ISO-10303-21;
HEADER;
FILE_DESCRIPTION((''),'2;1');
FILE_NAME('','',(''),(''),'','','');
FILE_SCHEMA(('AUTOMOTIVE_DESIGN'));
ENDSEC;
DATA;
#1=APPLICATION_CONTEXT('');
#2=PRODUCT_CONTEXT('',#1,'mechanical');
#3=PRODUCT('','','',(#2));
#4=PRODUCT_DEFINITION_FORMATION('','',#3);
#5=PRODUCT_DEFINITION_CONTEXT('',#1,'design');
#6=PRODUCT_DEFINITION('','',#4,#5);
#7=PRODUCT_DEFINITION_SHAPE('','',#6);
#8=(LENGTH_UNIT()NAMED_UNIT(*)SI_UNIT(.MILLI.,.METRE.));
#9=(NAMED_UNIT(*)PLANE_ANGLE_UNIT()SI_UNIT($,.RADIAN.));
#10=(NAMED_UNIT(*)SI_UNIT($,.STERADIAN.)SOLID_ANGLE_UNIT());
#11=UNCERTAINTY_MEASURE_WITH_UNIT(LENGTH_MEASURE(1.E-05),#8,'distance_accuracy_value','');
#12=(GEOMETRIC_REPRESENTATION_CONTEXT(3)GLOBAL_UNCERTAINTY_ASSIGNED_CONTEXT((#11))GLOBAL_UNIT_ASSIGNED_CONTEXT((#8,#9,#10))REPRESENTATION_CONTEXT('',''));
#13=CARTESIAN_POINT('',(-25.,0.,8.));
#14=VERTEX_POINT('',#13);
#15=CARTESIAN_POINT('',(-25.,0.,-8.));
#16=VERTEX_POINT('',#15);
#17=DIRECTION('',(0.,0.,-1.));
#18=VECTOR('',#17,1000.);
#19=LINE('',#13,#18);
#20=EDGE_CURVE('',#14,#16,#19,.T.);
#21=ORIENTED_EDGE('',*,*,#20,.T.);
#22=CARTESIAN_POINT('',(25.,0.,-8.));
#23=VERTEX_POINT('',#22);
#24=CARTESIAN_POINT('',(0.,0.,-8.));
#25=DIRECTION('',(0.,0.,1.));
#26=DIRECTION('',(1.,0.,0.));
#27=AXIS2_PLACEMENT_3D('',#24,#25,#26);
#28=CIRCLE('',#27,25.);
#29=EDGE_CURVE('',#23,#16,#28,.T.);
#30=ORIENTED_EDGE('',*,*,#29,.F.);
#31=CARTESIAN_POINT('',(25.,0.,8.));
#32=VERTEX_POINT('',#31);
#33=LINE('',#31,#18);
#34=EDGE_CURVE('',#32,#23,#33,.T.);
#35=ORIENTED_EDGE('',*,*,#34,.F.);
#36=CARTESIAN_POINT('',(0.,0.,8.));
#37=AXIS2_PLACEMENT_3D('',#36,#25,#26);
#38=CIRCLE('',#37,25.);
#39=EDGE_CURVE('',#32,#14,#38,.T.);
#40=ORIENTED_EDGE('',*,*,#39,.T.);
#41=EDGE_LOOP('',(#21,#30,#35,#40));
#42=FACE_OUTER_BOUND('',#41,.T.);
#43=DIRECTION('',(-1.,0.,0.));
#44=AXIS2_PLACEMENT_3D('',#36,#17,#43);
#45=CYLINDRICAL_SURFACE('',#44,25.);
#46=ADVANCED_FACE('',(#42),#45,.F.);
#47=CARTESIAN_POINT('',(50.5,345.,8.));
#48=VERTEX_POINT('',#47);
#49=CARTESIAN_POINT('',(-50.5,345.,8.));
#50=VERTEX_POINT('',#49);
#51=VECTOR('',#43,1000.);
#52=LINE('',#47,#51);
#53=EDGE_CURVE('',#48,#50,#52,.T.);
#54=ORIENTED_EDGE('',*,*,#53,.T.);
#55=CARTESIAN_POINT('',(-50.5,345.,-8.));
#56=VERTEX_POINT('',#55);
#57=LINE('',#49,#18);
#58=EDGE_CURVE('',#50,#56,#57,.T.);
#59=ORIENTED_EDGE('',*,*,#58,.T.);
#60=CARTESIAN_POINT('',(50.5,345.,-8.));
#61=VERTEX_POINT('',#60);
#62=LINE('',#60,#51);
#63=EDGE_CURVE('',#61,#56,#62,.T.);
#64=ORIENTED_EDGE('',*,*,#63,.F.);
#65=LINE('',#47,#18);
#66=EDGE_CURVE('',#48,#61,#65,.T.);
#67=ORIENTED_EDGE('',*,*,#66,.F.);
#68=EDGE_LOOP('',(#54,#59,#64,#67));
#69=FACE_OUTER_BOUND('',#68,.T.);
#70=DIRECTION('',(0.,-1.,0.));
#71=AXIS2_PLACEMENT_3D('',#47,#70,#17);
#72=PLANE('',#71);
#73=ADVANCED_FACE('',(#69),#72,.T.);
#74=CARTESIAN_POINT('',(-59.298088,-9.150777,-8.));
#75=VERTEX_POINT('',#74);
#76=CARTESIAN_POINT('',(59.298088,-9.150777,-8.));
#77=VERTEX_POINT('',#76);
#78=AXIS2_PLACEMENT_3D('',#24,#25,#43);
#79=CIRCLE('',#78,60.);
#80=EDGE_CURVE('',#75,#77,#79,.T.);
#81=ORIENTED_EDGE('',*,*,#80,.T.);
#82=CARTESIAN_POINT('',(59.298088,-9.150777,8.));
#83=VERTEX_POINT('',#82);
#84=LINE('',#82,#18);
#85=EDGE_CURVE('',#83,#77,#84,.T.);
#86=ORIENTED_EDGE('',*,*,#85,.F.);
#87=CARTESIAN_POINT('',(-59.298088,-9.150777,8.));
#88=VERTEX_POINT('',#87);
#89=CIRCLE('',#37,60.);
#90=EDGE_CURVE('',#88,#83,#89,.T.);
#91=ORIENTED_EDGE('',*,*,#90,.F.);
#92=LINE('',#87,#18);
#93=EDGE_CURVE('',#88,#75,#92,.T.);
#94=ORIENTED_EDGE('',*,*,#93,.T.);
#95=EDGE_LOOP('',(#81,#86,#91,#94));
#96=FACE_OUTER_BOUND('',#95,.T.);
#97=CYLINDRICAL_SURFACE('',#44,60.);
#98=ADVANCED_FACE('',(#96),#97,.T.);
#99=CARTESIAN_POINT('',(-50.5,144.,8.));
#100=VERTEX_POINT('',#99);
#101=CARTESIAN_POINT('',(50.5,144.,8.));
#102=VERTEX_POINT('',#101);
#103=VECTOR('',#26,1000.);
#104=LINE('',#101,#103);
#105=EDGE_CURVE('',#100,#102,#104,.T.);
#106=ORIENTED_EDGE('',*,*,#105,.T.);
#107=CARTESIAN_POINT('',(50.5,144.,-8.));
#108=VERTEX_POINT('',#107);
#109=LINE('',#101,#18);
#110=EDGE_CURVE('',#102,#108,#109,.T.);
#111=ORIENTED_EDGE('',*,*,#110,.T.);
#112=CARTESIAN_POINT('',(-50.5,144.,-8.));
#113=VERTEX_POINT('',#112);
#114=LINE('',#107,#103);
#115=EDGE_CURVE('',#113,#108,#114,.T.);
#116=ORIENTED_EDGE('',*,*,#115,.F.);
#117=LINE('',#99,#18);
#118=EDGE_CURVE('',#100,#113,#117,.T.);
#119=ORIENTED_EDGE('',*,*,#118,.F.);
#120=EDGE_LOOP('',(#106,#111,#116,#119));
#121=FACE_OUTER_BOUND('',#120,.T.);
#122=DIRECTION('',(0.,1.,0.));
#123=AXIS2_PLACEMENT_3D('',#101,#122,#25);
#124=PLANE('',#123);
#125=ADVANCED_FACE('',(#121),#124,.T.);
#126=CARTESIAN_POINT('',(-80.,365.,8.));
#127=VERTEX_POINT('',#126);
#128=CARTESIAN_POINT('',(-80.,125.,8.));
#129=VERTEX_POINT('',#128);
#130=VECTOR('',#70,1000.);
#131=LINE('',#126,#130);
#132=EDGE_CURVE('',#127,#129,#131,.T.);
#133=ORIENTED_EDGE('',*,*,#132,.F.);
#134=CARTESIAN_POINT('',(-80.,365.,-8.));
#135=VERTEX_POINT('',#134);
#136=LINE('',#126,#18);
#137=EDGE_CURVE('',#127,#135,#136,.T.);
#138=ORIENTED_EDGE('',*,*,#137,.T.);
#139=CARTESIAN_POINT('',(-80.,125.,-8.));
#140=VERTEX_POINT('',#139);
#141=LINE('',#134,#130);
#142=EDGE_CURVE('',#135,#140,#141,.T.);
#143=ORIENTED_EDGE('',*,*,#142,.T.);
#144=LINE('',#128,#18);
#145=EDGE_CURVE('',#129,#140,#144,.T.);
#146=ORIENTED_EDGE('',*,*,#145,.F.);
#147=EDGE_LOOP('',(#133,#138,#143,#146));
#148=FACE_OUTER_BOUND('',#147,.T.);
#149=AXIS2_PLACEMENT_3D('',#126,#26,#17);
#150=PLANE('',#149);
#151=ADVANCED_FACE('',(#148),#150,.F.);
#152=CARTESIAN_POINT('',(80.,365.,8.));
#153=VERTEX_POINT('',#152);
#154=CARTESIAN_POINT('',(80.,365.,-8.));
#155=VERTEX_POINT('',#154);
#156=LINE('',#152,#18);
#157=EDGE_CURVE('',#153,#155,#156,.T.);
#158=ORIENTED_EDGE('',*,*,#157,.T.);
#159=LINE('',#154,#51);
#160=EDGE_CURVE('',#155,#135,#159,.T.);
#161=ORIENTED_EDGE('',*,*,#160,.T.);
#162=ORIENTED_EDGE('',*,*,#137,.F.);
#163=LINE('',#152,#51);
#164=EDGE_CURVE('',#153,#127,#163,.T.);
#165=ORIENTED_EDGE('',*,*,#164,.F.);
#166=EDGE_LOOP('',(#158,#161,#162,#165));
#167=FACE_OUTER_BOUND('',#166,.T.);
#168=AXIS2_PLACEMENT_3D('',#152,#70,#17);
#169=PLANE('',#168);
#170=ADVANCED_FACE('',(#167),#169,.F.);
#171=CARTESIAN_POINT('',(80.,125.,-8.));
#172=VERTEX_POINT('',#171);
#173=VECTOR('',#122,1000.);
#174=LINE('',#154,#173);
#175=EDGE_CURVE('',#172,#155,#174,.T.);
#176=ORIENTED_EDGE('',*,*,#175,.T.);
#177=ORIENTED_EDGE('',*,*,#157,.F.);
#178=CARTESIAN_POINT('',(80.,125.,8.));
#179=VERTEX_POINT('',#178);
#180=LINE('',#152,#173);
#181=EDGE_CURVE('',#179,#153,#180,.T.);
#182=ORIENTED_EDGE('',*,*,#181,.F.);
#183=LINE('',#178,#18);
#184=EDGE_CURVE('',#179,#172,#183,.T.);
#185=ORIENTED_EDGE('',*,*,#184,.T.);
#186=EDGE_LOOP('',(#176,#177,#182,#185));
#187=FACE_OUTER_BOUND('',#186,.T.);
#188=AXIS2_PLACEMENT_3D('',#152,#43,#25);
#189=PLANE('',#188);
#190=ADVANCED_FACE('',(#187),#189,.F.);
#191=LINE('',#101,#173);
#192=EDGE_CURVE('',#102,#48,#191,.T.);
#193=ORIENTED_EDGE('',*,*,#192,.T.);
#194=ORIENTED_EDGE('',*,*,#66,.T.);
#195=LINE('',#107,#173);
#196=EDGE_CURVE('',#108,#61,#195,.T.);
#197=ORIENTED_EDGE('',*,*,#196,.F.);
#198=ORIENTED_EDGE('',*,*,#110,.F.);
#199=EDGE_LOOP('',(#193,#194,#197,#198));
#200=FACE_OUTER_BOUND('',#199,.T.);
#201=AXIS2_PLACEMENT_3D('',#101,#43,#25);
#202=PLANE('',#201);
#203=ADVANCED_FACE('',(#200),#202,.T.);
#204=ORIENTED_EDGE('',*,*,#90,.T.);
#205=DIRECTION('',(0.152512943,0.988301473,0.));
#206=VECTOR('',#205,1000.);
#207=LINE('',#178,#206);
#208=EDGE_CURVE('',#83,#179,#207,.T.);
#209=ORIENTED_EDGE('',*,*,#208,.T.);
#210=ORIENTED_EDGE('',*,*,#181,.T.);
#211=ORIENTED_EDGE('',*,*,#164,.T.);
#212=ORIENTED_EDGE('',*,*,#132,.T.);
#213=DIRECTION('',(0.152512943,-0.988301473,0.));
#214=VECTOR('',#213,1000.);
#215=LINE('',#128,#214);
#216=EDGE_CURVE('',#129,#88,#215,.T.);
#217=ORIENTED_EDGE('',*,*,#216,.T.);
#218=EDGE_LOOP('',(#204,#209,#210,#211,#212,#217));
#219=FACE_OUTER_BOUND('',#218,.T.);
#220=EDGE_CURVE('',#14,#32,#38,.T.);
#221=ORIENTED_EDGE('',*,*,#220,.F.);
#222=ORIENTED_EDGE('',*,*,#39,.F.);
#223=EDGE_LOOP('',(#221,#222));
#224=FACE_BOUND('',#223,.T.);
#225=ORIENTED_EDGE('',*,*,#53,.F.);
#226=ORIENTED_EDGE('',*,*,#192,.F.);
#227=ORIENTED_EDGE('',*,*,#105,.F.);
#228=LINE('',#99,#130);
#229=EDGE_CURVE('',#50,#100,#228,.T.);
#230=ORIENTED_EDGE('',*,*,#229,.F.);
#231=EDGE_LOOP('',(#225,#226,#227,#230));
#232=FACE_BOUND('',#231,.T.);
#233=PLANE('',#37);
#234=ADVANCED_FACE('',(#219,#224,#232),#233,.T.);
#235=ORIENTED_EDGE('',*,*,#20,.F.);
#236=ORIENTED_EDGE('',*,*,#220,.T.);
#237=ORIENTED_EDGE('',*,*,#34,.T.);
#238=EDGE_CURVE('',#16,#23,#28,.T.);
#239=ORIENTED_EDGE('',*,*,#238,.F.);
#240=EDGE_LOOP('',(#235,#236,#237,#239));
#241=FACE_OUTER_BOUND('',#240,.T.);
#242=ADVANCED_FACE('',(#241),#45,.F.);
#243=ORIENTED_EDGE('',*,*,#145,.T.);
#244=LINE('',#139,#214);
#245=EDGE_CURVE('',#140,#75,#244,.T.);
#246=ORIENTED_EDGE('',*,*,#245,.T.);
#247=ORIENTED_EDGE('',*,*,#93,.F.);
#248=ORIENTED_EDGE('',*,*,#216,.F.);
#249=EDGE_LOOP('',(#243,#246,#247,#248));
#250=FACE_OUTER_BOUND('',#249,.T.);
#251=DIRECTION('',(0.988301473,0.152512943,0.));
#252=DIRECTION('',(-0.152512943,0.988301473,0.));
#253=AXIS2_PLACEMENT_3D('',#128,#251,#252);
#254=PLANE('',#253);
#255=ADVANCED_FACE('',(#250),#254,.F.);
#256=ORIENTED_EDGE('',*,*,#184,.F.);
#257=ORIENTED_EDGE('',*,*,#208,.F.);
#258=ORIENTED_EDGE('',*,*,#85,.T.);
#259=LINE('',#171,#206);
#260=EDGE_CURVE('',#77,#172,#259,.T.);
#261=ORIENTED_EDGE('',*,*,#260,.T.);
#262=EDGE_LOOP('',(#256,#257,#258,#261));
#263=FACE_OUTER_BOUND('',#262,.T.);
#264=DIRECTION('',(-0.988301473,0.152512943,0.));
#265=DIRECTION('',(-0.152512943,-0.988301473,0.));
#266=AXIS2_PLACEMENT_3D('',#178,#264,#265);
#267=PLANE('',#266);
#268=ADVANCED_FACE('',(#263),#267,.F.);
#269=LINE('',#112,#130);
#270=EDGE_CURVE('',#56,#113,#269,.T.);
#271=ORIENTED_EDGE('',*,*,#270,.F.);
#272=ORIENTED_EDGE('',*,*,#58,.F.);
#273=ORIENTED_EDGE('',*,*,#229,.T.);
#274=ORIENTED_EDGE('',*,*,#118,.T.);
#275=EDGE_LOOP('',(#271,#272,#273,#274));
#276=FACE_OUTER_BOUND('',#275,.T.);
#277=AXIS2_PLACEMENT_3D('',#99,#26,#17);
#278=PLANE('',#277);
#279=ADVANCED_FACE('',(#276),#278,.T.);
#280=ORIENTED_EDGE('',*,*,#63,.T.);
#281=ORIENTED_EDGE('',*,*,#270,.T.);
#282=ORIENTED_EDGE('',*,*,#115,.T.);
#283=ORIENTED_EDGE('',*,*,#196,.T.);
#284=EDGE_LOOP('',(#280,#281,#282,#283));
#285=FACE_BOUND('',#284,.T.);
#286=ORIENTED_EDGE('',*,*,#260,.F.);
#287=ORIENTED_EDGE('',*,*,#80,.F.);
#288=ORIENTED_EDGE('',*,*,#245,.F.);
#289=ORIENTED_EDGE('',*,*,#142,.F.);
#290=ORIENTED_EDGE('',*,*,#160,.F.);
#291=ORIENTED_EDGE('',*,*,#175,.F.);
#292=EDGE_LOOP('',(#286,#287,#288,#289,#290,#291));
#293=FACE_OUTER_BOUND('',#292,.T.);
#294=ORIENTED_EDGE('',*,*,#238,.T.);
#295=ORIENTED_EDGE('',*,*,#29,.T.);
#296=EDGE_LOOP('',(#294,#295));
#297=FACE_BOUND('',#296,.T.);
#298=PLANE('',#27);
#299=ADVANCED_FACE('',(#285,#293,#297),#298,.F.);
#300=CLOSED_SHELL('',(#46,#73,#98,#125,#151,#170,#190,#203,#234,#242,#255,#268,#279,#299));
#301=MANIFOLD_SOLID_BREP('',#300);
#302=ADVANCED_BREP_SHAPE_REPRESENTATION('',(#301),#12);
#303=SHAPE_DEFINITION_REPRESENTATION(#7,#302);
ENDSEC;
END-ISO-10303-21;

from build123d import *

# Parameters (mm, degrees)
SKETCH1_R           = 25
SKETCH1_W           = 101
SKETCH1_H           = 201
BOSS_EXTRUDE1_DEPTH = 8


with BuildPart() as part:
    # Sketch1 → Boss-Extrude1 (new, symmetric)
    with BuildSketch(Plane.XY):
        with BuildLine():
            Line((80, 365), (-80, 365))
            Line((-80, 365), (-80, 125))
            Line((-80, 125), (-59.298088401, -9.150776577))
            ThreePointArc((-59.298088401, -9.150776577), (-39.057351455, -45.546935103), (0, -60))
            ThreePointArc((0, -60), (39.057351455, -45.546935103), (59.298088401, -9.150776577))
            Line((59.298088401, -9.150776577), (80, 125))
            Line((80, 125), (80, 365))
        make_face()
        Circle(SKETCH1_R, mode=Mode.SUBTRACT)
        with Locations((0, 244.5)):
            Rectangle(SKETCH1_W, SKETCH1_H, mode=Mode.SUBTRACT)
    extrude(amount=BOSS_EXTRUDE1_DEPTH, both=True)


solid = part.part
